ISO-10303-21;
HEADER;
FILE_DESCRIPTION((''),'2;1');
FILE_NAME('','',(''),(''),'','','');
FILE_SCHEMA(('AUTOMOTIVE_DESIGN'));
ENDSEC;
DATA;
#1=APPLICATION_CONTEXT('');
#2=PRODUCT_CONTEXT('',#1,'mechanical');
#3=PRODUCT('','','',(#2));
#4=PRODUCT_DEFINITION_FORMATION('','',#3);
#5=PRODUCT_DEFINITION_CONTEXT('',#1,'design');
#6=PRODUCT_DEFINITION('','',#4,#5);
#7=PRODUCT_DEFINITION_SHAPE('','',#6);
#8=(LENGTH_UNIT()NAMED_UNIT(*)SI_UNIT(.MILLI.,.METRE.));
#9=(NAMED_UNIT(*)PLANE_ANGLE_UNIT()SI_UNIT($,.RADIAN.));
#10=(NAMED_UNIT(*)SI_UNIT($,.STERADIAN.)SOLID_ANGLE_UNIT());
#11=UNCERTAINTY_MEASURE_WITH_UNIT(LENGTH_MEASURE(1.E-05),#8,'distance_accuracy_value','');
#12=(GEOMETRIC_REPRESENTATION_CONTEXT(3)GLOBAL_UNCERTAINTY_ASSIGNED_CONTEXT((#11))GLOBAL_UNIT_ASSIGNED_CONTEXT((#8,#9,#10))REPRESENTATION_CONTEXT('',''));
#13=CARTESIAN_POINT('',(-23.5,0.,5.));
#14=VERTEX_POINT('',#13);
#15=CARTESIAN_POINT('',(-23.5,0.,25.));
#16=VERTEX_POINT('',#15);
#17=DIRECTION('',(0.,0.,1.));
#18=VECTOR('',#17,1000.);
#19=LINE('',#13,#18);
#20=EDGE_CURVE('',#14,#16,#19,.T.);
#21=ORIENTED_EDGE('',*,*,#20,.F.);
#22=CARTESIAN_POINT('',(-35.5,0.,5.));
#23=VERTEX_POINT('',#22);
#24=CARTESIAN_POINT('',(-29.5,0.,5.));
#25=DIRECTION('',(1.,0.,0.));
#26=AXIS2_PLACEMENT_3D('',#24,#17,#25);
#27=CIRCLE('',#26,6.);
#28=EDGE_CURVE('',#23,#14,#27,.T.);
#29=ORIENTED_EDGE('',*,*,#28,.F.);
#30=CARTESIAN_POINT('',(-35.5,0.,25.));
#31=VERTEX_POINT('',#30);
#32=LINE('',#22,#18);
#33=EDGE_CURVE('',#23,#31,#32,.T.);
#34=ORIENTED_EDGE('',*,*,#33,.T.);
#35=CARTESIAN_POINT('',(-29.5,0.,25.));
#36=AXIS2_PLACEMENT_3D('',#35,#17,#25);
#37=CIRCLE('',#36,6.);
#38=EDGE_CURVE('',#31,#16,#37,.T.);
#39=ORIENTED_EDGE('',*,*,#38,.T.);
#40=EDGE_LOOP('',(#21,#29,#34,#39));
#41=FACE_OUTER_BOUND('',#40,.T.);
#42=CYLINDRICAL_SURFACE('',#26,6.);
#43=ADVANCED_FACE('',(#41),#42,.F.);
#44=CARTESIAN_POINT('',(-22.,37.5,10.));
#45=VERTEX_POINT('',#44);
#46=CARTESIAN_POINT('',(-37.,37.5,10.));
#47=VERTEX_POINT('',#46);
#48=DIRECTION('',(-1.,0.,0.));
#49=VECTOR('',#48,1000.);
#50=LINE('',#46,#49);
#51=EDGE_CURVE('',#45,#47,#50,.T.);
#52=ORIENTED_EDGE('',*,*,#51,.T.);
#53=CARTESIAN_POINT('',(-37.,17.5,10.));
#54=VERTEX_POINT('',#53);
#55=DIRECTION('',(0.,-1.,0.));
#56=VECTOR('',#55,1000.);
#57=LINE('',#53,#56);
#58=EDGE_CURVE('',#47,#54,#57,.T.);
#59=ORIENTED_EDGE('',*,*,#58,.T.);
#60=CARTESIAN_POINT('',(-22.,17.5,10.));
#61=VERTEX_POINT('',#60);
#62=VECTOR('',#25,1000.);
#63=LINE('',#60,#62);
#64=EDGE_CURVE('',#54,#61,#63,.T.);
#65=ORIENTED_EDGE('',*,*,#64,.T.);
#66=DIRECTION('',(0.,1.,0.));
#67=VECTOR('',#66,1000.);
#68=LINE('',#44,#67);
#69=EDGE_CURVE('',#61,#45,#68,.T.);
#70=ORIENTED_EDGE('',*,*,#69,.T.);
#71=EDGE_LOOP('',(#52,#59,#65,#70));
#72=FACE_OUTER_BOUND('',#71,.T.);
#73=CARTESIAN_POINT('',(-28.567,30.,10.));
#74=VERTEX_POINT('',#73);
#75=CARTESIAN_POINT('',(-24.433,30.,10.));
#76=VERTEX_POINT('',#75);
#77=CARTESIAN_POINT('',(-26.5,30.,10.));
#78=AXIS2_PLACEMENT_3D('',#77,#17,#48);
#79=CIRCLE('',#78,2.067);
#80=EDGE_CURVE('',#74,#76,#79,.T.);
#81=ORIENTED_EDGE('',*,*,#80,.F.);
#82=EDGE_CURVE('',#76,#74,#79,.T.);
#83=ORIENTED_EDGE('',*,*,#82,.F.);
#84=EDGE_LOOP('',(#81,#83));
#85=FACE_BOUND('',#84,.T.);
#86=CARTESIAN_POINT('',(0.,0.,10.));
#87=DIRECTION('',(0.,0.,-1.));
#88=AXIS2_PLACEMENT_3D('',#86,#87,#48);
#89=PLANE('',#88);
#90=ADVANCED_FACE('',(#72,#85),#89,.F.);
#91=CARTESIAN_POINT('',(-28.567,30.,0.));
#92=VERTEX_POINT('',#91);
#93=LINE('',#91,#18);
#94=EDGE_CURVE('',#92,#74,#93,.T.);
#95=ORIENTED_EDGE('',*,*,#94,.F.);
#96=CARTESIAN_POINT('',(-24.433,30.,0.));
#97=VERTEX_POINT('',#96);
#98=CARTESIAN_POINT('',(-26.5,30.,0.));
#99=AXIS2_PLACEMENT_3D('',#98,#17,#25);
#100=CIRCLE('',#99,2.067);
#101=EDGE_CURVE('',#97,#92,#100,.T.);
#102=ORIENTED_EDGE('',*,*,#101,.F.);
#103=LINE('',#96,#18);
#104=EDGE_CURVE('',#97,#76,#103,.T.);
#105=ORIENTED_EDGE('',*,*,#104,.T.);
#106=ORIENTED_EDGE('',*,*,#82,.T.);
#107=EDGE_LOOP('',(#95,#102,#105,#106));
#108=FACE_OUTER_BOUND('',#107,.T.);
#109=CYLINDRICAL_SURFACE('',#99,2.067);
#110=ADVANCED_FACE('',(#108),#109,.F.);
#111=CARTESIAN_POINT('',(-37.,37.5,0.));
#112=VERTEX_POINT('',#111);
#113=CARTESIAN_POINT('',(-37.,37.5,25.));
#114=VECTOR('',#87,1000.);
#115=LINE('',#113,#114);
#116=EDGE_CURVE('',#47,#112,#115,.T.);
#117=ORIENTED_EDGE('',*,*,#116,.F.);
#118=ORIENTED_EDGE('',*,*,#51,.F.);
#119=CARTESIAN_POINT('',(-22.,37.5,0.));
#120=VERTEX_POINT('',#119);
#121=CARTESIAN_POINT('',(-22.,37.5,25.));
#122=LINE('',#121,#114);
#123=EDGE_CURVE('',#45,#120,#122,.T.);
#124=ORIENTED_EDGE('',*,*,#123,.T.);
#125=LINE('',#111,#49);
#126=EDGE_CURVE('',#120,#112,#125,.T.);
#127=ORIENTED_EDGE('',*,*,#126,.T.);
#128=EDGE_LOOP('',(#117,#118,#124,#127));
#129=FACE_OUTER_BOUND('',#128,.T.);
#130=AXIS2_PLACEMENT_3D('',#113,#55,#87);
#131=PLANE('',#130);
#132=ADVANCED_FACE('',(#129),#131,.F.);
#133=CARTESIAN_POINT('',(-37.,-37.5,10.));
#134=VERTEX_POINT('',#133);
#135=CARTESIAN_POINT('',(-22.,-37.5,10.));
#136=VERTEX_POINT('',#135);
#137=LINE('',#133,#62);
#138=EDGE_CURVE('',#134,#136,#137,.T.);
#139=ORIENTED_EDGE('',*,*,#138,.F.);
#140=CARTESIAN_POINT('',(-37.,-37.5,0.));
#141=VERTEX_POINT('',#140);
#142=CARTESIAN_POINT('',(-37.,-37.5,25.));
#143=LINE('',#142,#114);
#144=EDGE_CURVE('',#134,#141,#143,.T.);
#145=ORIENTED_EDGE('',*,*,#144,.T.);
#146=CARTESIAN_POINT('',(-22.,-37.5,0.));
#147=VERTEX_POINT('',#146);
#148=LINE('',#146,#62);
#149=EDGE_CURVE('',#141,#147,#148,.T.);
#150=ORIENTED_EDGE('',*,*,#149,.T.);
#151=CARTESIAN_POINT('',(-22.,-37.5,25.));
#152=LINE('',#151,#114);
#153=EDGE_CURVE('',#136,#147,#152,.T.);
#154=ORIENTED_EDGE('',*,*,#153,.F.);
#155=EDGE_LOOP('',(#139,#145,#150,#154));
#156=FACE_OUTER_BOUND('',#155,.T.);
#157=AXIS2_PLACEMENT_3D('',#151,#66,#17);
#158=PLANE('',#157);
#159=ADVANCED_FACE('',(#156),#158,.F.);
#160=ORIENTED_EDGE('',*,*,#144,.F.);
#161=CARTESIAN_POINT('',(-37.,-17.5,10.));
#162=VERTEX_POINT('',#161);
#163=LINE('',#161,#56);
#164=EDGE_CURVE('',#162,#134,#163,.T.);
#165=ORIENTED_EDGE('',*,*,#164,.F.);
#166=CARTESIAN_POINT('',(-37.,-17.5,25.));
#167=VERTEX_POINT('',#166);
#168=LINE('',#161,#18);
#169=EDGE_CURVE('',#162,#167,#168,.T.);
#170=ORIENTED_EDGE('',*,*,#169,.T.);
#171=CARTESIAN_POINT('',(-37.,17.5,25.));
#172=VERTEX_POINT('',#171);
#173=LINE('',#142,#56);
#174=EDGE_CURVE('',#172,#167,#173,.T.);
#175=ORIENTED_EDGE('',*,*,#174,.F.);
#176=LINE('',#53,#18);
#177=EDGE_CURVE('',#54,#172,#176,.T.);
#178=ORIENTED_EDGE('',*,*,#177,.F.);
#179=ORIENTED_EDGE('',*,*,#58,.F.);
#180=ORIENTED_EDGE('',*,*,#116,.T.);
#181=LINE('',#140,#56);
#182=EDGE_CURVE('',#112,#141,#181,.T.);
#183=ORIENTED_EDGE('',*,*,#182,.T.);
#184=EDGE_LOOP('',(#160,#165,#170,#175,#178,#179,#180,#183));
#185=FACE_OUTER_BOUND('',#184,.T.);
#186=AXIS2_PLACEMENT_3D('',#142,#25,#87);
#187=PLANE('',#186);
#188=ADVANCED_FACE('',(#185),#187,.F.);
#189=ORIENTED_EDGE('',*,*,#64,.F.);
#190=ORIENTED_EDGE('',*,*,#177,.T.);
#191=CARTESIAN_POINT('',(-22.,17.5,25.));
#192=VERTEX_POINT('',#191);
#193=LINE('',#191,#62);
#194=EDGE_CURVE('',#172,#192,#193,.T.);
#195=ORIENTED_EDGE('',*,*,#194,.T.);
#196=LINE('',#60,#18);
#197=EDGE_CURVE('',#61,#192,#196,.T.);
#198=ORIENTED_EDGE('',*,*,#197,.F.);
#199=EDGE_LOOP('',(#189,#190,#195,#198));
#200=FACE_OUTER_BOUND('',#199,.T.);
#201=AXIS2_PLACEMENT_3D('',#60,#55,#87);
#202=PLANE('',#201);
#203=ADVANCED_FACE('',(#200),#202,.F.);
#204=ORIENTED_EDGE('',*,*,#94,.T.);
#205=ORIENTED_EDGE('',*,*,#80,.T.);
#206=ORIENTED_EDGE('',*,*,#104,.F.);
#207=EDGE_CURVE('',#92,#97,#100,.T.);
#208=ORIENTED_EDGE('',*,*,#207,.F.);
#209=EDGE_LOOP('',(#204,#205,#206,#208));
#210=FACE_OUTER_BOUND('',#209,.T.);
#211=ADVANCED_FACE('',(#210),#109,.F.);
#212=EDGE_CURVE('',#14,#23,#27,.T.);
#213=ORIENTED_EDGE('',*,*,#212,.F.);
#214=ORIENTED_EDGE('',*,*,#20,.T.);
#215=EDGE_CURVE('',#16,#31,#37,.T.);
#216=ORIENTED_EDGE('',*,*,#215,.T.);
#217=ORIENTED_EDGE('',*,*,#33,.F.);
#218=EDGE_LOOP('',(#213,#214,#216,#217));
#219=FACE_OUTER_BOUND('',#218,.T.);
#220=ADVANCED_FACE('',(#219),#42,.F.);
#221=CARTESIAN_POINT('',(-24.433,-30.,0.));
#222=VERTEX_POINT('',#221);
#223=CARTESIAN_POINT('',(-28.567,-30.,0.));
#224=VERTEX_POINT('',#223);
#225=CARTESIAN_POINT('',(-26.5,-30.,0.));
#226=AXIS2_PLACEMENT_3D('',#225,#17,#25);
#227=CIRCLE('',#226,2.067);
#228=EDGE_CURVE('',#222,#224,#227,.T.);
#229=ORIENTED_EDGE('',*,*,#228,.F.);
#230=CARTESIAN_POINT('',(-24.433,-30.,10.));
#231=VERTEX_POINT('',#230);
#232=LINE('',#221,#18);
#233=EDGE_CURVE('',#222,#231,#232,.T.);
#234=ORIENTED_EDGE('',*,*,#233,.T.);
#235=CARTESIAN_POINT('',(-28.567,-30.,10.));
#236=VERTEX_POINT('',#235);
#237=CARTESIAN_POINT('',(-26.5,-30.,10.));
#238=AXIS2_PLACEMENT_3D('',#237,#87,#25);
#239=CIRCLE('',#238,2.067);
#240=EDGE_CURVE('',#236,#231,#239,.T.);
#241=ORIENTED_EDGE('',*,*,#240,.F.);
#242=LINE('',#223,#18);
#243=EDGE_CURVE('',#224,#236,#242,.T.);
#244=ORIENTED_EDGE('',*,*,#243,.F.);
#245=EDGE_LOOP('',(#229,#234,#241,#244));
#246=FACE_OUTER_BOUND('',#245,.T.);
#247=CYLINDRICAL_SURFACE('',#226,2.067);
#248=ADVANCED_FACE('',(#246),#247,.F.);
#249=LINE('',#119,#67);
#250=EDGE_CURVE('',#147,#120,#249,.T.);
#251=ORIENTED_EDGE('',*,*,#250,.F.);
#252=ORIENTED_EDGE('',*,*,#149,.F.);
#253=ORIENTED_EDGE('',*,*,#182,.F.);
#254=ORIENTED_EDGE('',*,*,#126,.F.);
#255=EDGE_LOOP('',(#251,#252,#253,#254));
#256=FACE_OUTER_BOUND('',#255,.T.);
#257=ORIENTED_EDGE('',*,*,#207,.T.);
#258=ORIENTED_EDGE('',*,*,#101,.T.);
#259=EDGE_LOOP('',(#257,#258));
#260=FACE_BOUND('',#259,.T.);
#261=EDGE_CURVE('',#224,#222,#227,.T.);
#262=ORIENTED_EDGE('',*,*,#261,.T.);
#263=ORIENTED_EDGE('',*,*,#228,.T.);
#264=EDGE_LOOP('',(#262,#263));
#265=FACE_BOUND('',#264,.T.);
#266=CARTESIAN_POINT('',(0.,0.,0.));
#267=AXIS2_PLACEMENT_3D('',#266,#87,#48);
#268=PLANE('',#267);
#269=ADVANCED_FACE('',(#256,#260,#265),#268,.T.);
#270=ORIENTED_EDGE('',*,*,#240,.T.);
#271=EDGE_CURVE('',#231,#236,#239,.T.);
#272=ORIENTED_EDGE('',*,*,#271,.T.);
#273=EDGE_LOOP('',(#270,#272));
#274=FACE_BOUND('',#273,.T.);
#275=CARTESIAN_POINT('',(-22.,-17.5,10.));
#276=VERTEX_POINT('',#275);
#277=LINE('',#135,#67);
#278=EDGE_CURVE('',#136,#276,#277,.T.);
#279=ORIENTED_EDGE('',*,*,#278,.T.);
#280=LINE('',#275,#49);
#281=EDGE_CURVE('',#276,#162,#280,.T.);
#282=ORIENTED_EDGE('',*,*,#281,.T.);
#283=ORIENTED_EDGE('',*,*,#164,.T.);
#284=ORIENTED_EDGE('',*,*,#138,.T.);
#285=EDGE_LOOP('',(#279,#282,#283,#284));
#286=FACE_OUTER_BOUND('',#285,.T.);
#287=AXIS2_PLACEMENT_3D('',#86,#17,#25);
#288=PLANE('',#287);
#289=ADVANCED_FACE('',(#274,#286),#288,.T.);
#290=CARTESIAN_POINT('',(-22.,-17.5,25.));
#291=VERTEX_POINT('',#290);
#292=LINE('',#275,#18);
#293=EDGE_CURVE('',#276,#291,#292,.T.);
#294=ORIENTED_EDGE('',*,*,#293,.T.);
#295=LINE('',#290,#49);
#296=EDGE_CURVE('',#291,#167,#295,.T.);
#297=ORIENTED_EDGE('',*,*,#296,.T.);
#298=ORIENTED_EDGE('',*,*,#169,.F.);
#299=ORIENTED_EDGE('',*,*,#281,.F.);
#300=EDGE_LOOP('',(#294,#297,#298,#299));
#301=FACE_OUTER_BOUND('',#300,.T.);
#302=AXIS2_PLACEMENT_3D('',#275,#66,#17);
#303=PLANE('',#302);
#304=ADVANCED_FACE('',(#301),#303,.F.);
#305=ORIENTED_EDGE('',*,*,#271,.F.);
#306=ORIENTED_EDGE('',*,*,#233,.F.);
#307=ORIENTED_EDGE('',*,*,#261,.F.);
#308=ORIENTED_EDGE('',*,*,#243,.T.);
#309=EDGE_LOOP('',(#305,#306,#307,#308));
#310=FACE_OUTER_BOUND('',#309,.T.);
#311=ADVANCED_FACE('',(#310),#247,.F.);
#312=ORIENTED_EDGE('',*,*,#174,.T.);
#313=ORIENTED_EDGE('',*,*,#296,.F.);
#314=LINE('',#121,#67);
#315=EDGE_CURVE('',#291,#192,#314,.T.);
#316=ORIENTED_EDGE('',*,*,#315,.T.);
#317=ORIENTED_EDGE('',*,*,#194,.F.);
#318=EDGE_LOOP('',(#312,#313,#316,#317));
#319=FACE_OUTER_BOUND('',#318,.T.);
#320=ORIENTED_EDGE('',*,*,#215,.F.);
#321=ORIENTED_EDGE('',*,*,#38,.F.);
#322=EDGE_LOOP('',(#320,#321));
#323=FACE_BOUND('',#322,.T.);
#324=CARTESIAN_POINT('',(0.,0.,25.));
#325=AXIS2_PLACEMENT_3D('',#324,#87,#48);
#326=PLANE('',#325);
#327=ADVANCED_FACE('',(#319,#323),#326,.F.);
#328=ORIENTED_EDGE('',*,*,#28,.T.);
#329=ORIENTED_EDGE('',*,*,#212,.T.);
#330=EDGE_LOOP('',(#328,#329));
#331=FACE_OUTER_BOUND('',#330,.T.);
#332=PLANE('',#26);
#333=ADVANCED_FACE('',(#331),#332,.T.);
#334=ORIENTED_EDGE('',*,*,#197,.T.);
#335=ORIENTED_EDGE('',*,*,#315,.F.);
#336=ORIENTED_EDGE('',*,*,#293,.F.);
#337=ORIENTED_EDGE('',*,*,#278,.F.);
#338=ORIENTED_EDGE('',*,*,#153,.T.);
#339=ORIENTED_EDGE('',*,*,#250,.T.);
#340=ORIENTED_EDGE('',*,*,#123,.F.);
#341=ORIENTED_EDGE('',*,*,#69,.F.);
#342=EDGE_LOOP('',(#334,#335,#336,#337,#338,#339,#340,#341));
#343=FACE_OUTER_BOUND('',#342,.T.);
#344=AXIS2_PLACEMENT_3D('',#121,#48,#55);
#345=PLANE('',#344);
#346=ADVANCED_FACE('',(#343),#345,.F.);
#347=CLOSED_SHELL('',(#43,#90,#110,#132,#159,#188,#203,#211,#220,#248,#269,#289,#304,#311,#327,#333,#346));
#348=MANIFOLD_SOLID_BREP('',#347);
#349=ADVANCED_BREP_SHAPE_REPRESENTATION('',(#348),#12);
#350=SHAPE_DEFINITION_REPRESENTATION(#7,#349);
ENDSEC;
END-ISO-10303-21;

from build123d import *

# Parameters (mm, degrees)
SKETCH1_W           = 15
SKETCH1_H           = 75
BOSS_EXTRUDE1_DEPTH = 25
SKETCH2_R           = 2.067
CUT_EXTRUDE1_DEPTH  = 25
SKETCH3_W           = 15
SKETCH3_H           = 20
CUT_EXTRUDE2_DEPTH  = 15
SKETCH4_R           = 6
CUT_EXTRUDE3_DEPTH  = 20


with BuildPart() as part:
    # Sketch1 → Boss-Extrude1 (new body)
    with BuildSketch(Plane.XY):
        with Locations((-29.5, 0)):
            Rectangle(SKETCH1_W, SKETCH1_H)
    extrude(amount=BOSS_EXTRUDE1_DEPTH)

    # Sketch2 → Cut-Extrude1 (cut)
    with BuildSketch(Plane.XY.offset(25)):
        with Locations((-26.5, 30)):
            Circle(SKETCH2_R)
        with Locations((-26.5, -30)):
            Circle(SKETCH2_R)
    extrude(amount=-CUT_EXTRUDE1_DEPTH, mode=Mode.SUBTRACT)

    # Sketch3 → Cut-Extrude2 (cut)
    with BuildSketch(Plane.XY.offset(25)):
        with Locations((-29.5, 27.5)):
            Rectangle(SKETCH3_W, SKETCH3_H)
        with Locations((-29.5, -27.5)):
            Rectangle(SKETCH3_W, SKETCH3_H)
    extrude(amount=-CUT_EXTRUDE2_DEPTH, mode=Mode.SUBTRACT)

    # Sketch4 → Cut-Extrude3 (cut)
    with BuildSketch(Plane.XY.offset(25)):
        with Locations((-29.5, 0)):
            Circle(SKETCH4_R)
    extrude(amount=-CUT_EXTRUDE3_DEPTH, mode=Mode.SUBTRACT)


solid = part.part
